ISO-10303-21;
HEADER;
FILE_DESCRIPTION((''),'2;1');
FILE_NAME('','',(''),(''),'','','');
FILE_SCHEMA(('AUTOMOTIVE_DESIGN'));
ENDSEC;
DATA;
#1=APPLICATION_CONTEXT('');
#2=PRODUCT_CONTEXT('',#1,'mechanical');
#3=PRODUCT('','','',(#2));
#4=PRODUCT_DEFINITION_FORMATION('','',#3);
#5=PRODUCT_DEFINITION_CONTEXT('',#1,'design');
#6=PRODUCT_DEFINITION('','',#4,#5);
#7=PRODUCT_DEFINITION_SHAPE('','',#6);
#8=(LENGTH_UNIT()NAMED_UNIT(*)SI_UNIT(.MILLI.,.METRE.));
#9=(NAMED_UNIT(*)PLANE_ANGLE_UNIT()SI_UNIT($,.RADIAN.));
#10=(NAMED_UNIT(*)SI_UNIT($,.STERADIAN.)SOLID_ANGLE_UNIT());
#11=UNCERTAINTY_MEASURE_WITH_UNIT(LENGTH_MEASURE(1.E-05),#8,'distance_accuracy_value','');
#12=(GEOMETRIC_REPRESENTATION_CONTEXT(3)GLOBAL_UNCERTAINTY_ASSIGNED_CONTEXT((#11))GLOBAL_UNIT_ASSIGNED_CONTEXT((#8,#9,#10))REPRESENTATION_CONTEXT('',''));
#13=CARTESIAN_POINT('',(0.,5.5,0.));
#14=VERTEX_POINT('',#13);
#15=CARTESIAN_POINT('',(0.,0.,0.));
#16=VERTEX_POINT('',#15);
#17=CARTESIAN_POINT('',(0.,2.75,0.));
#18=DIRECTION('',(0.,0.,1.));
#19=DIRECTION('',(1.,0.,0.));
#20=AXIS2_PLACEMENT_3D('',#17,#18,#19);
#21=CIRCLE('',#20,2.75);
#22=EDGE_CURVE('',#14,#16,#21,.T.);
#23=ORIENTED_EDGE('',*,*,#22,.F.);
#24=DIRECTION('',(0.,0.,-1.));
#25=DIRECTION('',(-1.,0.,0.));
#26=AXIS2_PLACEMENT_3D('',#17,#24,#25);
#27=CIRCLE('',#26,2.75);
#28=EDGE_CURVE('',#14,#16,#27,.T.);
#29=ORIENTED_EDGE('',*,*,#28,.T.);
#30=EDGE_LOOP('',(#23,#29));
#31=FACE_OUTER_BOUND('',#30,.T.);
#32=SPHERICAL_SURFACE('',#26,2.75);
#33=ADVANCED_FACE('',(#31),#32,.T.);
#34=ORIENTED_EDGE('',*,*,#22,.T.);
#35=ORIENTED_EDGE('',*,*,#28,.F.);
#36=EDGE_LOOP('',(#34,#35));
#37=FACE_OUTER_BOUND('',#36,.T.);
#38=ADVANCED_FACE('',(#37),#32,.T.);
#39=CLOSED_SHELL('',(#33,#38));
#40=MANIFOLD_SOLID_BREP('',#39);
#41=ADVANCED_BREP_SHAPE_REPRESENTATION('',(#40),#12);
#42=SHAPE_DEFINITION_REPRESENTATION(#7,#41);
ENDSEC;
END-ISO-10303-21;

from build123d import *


with BuildPart() as part:
    # Sketch1 → Revolve1 (revolve)
    with BuildSketch(Plane.XY):
        with BuildLine():
            Line((0, 0), (0, 5.5))
            ThreePointArc((0, 5.5), (-2.75, 2.75), (0, 0))
        make_face()
    revolve(axis=Axis((0, 0, 0), (0, 1, 0)))


solid = part.part
